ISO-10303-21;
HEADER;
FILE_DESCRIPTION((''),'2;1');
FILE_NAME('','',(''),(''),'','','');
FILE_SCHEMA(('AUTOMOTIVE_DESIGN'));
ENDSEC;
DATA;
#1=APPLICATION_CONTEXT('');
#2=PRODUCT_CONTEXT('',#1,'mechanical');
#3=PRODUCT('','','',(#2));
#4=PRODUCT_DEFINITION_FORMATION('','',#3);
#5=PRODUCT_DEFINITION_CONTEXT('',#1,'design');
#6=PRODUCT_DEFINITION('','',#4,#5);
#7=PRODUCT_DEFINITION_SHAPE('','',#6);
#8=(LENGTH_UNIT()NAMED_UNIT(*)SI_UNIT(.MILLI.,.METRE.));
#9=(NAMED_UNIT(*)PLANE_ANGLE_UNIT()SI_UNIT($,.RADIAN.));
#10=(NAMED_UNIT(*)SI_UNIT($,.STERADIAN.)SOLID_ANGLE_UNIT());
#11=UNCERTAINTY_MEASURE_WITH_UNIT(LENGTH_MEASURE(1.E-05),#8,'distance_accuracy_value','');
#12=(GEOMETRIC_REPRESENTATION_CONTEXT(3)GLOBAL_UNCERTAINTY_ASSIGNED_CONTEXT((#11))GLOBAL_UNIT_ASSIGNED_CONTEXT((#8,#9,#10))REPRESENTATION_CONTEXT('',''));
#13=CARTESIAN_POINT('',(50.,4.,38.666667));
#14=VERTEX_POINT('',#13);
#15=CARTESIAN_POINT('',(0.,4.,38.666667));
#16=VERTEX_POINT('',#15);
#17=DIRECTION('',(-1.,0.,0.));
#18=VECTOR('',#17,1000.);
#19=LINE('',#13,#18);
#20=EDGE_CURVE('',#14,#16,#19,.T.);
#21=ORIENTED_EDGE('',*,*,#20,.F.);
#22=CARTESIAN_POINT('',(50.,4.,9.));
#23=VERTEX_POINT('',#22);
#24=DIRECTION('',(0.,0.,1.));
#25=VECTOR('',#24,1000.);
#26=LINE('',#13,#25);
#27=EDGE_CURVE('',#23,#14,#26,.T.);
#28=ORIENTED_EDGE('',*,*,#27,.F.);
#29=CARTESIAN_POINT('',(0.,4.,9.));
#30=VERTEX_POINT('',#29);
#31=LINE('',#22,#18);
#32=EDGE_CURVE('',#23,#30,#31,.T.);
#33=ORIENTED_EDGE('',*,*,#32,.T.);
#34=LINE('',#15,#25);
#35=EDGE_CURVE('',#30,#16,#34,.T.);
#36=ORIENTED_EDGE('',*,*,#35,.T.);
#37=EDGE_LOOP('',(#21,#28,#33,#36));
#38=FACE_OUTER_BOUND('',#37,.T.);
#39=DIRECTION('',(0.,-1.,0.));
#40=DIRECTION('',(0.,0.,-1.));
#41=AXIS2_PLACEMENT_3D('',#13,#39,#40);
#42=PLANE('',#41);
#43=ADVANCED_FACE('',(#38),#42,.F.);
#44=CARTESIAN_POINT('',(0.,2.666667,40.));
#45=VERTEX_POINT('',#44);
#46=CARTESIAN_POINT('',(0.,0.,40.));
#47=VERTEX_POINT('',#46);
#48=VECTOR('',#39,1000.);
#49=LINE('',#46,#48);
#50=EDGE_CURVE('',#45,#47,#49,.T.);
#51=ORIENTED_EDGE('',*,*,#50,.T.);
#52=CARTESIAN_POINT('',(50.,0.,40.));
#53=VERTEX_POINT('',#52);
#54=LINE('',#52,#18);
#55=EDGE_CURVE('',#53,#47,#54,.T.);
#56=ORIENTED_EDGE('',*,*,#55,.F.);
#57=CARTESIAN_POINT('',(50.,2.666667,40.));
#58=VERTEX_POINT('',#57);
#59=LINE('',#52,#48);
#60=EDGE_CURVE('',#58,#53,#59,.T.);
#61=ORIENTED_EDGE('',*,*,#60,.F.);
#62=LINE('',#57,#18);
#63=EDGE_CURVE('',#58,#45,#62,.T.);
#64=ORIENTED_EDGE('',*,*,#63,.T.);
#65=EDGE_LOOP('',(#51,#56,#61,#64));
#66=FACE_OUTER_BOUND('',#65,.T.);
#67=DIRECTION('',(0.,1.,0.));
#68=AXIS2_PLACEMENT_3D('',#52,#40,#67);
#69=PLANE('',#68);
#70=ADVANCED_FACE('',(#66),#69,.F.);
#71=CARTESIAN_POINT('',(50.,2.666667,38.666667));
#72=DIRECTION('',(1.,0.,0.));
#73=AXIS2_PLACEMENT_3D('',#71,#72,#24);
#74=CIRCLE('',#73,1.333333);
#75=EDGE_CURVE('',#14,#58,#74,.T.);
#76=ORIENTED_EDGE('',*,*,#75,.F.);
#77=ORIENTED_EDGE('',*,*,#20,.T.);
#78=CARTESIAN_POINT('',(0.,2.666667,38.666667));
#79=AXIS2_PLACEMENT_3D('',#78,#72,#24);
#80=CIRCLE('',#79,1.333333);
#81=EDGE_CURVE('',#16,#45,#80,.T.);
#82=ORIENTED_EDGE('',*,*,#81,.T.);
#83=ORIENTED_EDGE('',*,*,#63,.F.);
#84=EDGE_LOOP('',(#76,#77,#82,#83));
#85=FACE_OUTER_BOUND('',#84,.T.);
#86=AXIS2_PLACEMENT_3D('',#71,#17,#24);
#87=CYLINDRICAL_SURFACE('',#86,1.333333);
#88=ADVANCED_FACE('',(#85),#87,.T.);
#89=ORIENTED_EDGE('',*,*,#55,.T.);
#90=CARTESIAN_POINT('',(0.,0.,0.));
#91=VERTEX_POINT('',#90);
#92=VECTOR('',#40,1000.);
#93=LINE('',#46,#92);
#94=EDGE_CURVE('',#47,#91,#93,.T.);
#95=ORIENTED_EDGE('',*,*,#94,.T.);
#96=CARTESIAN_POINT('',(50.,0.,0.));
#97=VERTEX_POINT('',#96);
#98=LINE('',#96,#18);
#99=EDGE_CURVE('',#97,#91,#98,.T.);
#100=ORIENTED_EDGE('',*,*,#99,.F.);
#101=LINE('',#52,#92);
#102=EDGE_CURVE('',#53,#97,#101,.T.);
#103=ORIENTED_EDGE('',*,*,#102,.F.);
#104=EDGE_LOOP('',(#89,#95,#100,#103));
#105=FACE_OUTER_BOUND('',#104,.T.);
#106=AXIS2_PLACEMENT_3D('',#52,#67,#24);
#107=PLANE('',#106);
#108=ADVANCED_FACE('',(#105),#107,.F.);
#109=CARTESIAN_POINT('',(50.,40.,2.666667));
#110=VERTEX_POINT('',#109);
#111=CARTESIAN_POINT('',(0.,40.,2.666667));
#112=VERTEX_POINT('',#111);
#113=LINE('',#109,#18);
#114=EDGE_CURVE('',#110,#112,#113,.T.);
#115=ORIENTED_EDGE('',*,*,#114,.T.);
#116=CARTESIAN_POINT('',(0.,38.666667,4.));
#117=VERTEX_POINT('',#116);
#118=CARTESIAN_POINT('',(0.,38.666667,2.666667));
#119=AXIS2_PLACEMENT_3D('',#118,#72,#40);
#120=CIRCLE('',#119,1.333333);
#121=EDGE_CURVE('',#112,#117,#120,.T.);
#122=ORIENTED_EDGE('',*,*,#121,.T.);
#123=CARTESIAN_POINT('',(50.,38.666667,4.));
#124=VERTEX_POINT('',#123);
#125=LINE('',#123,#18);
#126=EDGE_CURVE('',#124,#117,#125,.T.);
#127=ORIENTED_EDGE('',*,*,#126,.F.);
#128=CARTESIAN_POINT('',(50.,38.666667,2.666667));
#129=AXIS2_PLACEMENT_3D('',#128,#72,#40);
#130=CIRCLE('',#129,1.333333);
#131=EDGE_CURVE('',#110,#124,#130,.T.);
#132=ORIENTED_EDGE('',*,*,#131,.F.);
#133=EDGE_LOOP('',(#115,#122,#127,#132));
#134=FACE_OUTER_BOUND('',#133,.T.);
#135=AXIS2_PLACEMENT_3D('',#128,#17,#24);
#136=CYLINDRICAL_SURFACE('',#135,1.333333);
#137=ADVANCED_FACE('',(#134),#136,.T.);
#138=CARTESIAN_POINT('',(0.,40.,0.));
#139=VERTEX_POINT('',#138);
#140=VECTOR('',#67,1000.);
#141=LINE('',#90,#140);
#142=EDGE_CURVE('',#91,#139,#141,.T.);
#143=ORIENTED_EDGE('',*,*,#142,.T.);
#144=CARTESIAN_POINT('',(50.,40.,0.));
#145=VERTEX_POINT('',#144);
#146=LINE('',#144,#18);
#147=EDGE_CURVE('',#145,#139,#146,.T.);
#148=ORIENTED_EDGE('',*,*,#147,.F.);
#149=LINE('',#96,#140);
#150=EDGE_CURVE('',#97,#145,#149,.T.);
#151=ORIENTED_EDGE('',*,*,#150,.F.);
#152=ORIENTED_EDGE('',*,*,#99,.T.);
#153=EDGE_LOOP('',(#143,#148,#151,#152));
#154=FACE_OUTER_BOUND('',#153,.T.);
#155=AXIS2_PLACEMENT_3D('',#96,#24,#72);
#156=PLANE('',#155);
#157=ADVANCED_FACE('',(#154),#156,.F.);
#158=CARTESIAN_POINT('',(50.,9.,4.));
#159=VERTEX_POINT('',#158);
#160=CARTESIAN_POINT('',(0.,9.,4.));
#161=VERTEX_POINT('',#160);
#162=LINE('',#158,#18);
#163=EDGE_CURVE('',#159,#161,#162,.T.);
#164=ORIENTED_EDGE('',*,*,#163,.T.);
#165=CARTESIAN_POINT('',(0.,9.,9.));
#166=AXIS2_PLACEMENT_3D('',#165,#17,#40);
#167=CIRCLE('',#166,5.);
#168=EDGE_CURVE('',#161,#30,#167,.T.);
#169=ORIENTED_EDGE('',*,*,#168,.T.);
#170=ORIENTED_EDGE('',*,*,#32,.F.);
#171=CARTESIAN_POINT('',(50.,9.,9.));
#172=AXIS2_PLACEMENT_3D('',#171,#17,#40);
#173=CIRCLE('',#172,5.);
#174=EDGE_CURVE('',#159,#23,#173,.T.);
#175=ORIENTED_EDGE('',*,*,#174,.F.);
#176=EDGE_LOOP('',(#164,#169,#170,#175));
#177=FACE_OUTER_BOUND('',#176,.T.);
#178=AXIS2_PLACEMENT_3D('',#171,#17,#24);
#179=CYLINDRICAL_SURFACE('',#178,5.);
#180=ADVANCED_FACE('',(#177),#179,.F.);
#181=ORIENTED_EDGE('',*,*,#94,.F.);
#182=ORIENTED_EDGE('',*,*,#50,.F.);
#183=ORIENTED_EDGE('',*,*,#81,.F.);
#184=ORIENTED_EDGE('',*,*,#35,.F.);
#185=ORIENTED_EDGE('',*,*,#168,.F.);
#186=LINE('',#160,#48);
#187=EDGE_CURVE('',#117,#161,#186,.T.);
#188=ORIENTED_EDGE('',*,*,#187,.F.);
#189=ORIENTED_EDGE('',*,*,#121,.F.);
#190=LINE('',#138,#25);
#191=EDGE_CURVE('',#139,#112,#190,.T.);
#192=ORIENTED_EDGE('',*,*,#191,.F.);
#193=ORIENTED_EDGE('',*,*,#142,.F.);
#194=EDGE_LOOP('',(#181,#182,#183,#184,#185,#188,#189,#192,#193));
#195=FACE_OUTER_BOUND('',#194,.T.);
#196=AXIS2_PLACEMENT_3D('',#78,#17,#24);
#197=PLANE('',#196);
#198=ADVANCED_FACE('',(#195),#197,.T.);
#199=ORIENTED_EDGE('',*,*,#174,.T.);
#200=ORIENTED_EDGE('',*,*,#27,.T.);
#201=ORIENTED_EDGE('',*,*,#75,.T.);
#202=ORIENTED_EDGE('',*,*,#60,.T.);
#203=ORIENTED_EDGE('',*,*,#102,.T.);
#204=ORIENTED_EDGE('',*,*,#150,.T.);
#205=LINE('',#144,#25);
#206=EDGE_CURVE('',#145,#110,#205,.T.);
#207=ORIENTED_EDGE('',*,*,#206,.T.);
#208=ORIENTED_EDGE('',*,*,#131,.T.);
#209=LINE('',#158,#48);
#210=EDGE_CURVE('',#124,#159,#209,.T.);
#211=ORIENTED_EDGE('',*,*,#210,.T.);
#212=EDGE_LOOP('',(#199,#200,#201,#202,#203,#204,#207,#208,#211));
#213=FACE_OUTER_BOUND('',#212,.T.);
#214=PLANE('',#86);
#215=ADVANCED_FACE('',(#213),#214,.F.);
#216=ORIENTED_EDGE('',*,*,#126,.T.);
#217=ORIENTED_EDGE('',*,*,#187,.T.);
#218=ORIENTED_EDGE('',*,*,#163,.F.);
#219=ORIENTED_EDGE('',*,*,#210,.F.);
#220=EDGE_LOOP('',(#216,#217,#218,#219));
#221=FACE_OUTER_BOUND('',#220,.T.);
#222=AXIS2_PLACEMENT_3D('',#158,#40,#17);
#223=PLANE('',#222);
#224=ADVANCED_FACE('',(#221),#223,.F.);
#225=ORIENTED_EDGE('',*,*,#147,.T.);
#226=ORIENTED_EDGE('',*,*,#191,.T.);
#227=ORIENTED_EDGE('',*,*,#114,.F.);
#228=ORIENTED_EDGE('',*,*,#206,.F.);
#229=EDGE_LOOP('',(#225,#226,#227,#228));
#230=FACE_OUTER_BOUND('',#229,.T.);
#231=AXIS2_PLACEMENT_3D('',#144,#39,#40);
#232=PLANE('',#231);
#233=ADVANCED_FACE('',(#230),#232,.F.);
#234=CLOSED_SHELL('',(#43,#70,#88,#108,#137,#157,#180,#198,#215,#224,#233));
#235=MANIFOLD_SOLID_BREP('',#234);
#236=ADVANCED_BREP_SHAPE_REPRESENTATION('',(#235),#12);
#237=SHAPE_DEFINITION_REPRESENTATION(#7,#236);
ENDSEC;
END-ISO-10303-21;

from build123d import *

# Parameters (mm, degrees)
BASE_DEPTH = 50


with BuildPart() as part:
    # Sketch1 → Base (new body)
    with BuildSketch(Plane.YZ):
        with BuildLine():
            Line((0, 40), (0, 0))
            Line((0, 0), (40, 0))
            Line((40, 0), (40, 2.666666667))
            ThreePointArc((40, 2.666666667), (39.609475708, 3.609475708), (38.666666667, 4))
            Line((38.666666667, 4), (9, 4))
            ThreePointArc((9, 4), (5.464466094, 5.464466094), (4, 9))
            Line((4, 9), (4, 38.666666667))
            ThreePointArc((4, 38.666666667), (3.609475708, 39.609475708), (2.666666667, 40))
            Line((2.666666667, 40), (0, 40))
        make_face()
    extrude(amount=BASE_DEPTH)


solid = part.part
